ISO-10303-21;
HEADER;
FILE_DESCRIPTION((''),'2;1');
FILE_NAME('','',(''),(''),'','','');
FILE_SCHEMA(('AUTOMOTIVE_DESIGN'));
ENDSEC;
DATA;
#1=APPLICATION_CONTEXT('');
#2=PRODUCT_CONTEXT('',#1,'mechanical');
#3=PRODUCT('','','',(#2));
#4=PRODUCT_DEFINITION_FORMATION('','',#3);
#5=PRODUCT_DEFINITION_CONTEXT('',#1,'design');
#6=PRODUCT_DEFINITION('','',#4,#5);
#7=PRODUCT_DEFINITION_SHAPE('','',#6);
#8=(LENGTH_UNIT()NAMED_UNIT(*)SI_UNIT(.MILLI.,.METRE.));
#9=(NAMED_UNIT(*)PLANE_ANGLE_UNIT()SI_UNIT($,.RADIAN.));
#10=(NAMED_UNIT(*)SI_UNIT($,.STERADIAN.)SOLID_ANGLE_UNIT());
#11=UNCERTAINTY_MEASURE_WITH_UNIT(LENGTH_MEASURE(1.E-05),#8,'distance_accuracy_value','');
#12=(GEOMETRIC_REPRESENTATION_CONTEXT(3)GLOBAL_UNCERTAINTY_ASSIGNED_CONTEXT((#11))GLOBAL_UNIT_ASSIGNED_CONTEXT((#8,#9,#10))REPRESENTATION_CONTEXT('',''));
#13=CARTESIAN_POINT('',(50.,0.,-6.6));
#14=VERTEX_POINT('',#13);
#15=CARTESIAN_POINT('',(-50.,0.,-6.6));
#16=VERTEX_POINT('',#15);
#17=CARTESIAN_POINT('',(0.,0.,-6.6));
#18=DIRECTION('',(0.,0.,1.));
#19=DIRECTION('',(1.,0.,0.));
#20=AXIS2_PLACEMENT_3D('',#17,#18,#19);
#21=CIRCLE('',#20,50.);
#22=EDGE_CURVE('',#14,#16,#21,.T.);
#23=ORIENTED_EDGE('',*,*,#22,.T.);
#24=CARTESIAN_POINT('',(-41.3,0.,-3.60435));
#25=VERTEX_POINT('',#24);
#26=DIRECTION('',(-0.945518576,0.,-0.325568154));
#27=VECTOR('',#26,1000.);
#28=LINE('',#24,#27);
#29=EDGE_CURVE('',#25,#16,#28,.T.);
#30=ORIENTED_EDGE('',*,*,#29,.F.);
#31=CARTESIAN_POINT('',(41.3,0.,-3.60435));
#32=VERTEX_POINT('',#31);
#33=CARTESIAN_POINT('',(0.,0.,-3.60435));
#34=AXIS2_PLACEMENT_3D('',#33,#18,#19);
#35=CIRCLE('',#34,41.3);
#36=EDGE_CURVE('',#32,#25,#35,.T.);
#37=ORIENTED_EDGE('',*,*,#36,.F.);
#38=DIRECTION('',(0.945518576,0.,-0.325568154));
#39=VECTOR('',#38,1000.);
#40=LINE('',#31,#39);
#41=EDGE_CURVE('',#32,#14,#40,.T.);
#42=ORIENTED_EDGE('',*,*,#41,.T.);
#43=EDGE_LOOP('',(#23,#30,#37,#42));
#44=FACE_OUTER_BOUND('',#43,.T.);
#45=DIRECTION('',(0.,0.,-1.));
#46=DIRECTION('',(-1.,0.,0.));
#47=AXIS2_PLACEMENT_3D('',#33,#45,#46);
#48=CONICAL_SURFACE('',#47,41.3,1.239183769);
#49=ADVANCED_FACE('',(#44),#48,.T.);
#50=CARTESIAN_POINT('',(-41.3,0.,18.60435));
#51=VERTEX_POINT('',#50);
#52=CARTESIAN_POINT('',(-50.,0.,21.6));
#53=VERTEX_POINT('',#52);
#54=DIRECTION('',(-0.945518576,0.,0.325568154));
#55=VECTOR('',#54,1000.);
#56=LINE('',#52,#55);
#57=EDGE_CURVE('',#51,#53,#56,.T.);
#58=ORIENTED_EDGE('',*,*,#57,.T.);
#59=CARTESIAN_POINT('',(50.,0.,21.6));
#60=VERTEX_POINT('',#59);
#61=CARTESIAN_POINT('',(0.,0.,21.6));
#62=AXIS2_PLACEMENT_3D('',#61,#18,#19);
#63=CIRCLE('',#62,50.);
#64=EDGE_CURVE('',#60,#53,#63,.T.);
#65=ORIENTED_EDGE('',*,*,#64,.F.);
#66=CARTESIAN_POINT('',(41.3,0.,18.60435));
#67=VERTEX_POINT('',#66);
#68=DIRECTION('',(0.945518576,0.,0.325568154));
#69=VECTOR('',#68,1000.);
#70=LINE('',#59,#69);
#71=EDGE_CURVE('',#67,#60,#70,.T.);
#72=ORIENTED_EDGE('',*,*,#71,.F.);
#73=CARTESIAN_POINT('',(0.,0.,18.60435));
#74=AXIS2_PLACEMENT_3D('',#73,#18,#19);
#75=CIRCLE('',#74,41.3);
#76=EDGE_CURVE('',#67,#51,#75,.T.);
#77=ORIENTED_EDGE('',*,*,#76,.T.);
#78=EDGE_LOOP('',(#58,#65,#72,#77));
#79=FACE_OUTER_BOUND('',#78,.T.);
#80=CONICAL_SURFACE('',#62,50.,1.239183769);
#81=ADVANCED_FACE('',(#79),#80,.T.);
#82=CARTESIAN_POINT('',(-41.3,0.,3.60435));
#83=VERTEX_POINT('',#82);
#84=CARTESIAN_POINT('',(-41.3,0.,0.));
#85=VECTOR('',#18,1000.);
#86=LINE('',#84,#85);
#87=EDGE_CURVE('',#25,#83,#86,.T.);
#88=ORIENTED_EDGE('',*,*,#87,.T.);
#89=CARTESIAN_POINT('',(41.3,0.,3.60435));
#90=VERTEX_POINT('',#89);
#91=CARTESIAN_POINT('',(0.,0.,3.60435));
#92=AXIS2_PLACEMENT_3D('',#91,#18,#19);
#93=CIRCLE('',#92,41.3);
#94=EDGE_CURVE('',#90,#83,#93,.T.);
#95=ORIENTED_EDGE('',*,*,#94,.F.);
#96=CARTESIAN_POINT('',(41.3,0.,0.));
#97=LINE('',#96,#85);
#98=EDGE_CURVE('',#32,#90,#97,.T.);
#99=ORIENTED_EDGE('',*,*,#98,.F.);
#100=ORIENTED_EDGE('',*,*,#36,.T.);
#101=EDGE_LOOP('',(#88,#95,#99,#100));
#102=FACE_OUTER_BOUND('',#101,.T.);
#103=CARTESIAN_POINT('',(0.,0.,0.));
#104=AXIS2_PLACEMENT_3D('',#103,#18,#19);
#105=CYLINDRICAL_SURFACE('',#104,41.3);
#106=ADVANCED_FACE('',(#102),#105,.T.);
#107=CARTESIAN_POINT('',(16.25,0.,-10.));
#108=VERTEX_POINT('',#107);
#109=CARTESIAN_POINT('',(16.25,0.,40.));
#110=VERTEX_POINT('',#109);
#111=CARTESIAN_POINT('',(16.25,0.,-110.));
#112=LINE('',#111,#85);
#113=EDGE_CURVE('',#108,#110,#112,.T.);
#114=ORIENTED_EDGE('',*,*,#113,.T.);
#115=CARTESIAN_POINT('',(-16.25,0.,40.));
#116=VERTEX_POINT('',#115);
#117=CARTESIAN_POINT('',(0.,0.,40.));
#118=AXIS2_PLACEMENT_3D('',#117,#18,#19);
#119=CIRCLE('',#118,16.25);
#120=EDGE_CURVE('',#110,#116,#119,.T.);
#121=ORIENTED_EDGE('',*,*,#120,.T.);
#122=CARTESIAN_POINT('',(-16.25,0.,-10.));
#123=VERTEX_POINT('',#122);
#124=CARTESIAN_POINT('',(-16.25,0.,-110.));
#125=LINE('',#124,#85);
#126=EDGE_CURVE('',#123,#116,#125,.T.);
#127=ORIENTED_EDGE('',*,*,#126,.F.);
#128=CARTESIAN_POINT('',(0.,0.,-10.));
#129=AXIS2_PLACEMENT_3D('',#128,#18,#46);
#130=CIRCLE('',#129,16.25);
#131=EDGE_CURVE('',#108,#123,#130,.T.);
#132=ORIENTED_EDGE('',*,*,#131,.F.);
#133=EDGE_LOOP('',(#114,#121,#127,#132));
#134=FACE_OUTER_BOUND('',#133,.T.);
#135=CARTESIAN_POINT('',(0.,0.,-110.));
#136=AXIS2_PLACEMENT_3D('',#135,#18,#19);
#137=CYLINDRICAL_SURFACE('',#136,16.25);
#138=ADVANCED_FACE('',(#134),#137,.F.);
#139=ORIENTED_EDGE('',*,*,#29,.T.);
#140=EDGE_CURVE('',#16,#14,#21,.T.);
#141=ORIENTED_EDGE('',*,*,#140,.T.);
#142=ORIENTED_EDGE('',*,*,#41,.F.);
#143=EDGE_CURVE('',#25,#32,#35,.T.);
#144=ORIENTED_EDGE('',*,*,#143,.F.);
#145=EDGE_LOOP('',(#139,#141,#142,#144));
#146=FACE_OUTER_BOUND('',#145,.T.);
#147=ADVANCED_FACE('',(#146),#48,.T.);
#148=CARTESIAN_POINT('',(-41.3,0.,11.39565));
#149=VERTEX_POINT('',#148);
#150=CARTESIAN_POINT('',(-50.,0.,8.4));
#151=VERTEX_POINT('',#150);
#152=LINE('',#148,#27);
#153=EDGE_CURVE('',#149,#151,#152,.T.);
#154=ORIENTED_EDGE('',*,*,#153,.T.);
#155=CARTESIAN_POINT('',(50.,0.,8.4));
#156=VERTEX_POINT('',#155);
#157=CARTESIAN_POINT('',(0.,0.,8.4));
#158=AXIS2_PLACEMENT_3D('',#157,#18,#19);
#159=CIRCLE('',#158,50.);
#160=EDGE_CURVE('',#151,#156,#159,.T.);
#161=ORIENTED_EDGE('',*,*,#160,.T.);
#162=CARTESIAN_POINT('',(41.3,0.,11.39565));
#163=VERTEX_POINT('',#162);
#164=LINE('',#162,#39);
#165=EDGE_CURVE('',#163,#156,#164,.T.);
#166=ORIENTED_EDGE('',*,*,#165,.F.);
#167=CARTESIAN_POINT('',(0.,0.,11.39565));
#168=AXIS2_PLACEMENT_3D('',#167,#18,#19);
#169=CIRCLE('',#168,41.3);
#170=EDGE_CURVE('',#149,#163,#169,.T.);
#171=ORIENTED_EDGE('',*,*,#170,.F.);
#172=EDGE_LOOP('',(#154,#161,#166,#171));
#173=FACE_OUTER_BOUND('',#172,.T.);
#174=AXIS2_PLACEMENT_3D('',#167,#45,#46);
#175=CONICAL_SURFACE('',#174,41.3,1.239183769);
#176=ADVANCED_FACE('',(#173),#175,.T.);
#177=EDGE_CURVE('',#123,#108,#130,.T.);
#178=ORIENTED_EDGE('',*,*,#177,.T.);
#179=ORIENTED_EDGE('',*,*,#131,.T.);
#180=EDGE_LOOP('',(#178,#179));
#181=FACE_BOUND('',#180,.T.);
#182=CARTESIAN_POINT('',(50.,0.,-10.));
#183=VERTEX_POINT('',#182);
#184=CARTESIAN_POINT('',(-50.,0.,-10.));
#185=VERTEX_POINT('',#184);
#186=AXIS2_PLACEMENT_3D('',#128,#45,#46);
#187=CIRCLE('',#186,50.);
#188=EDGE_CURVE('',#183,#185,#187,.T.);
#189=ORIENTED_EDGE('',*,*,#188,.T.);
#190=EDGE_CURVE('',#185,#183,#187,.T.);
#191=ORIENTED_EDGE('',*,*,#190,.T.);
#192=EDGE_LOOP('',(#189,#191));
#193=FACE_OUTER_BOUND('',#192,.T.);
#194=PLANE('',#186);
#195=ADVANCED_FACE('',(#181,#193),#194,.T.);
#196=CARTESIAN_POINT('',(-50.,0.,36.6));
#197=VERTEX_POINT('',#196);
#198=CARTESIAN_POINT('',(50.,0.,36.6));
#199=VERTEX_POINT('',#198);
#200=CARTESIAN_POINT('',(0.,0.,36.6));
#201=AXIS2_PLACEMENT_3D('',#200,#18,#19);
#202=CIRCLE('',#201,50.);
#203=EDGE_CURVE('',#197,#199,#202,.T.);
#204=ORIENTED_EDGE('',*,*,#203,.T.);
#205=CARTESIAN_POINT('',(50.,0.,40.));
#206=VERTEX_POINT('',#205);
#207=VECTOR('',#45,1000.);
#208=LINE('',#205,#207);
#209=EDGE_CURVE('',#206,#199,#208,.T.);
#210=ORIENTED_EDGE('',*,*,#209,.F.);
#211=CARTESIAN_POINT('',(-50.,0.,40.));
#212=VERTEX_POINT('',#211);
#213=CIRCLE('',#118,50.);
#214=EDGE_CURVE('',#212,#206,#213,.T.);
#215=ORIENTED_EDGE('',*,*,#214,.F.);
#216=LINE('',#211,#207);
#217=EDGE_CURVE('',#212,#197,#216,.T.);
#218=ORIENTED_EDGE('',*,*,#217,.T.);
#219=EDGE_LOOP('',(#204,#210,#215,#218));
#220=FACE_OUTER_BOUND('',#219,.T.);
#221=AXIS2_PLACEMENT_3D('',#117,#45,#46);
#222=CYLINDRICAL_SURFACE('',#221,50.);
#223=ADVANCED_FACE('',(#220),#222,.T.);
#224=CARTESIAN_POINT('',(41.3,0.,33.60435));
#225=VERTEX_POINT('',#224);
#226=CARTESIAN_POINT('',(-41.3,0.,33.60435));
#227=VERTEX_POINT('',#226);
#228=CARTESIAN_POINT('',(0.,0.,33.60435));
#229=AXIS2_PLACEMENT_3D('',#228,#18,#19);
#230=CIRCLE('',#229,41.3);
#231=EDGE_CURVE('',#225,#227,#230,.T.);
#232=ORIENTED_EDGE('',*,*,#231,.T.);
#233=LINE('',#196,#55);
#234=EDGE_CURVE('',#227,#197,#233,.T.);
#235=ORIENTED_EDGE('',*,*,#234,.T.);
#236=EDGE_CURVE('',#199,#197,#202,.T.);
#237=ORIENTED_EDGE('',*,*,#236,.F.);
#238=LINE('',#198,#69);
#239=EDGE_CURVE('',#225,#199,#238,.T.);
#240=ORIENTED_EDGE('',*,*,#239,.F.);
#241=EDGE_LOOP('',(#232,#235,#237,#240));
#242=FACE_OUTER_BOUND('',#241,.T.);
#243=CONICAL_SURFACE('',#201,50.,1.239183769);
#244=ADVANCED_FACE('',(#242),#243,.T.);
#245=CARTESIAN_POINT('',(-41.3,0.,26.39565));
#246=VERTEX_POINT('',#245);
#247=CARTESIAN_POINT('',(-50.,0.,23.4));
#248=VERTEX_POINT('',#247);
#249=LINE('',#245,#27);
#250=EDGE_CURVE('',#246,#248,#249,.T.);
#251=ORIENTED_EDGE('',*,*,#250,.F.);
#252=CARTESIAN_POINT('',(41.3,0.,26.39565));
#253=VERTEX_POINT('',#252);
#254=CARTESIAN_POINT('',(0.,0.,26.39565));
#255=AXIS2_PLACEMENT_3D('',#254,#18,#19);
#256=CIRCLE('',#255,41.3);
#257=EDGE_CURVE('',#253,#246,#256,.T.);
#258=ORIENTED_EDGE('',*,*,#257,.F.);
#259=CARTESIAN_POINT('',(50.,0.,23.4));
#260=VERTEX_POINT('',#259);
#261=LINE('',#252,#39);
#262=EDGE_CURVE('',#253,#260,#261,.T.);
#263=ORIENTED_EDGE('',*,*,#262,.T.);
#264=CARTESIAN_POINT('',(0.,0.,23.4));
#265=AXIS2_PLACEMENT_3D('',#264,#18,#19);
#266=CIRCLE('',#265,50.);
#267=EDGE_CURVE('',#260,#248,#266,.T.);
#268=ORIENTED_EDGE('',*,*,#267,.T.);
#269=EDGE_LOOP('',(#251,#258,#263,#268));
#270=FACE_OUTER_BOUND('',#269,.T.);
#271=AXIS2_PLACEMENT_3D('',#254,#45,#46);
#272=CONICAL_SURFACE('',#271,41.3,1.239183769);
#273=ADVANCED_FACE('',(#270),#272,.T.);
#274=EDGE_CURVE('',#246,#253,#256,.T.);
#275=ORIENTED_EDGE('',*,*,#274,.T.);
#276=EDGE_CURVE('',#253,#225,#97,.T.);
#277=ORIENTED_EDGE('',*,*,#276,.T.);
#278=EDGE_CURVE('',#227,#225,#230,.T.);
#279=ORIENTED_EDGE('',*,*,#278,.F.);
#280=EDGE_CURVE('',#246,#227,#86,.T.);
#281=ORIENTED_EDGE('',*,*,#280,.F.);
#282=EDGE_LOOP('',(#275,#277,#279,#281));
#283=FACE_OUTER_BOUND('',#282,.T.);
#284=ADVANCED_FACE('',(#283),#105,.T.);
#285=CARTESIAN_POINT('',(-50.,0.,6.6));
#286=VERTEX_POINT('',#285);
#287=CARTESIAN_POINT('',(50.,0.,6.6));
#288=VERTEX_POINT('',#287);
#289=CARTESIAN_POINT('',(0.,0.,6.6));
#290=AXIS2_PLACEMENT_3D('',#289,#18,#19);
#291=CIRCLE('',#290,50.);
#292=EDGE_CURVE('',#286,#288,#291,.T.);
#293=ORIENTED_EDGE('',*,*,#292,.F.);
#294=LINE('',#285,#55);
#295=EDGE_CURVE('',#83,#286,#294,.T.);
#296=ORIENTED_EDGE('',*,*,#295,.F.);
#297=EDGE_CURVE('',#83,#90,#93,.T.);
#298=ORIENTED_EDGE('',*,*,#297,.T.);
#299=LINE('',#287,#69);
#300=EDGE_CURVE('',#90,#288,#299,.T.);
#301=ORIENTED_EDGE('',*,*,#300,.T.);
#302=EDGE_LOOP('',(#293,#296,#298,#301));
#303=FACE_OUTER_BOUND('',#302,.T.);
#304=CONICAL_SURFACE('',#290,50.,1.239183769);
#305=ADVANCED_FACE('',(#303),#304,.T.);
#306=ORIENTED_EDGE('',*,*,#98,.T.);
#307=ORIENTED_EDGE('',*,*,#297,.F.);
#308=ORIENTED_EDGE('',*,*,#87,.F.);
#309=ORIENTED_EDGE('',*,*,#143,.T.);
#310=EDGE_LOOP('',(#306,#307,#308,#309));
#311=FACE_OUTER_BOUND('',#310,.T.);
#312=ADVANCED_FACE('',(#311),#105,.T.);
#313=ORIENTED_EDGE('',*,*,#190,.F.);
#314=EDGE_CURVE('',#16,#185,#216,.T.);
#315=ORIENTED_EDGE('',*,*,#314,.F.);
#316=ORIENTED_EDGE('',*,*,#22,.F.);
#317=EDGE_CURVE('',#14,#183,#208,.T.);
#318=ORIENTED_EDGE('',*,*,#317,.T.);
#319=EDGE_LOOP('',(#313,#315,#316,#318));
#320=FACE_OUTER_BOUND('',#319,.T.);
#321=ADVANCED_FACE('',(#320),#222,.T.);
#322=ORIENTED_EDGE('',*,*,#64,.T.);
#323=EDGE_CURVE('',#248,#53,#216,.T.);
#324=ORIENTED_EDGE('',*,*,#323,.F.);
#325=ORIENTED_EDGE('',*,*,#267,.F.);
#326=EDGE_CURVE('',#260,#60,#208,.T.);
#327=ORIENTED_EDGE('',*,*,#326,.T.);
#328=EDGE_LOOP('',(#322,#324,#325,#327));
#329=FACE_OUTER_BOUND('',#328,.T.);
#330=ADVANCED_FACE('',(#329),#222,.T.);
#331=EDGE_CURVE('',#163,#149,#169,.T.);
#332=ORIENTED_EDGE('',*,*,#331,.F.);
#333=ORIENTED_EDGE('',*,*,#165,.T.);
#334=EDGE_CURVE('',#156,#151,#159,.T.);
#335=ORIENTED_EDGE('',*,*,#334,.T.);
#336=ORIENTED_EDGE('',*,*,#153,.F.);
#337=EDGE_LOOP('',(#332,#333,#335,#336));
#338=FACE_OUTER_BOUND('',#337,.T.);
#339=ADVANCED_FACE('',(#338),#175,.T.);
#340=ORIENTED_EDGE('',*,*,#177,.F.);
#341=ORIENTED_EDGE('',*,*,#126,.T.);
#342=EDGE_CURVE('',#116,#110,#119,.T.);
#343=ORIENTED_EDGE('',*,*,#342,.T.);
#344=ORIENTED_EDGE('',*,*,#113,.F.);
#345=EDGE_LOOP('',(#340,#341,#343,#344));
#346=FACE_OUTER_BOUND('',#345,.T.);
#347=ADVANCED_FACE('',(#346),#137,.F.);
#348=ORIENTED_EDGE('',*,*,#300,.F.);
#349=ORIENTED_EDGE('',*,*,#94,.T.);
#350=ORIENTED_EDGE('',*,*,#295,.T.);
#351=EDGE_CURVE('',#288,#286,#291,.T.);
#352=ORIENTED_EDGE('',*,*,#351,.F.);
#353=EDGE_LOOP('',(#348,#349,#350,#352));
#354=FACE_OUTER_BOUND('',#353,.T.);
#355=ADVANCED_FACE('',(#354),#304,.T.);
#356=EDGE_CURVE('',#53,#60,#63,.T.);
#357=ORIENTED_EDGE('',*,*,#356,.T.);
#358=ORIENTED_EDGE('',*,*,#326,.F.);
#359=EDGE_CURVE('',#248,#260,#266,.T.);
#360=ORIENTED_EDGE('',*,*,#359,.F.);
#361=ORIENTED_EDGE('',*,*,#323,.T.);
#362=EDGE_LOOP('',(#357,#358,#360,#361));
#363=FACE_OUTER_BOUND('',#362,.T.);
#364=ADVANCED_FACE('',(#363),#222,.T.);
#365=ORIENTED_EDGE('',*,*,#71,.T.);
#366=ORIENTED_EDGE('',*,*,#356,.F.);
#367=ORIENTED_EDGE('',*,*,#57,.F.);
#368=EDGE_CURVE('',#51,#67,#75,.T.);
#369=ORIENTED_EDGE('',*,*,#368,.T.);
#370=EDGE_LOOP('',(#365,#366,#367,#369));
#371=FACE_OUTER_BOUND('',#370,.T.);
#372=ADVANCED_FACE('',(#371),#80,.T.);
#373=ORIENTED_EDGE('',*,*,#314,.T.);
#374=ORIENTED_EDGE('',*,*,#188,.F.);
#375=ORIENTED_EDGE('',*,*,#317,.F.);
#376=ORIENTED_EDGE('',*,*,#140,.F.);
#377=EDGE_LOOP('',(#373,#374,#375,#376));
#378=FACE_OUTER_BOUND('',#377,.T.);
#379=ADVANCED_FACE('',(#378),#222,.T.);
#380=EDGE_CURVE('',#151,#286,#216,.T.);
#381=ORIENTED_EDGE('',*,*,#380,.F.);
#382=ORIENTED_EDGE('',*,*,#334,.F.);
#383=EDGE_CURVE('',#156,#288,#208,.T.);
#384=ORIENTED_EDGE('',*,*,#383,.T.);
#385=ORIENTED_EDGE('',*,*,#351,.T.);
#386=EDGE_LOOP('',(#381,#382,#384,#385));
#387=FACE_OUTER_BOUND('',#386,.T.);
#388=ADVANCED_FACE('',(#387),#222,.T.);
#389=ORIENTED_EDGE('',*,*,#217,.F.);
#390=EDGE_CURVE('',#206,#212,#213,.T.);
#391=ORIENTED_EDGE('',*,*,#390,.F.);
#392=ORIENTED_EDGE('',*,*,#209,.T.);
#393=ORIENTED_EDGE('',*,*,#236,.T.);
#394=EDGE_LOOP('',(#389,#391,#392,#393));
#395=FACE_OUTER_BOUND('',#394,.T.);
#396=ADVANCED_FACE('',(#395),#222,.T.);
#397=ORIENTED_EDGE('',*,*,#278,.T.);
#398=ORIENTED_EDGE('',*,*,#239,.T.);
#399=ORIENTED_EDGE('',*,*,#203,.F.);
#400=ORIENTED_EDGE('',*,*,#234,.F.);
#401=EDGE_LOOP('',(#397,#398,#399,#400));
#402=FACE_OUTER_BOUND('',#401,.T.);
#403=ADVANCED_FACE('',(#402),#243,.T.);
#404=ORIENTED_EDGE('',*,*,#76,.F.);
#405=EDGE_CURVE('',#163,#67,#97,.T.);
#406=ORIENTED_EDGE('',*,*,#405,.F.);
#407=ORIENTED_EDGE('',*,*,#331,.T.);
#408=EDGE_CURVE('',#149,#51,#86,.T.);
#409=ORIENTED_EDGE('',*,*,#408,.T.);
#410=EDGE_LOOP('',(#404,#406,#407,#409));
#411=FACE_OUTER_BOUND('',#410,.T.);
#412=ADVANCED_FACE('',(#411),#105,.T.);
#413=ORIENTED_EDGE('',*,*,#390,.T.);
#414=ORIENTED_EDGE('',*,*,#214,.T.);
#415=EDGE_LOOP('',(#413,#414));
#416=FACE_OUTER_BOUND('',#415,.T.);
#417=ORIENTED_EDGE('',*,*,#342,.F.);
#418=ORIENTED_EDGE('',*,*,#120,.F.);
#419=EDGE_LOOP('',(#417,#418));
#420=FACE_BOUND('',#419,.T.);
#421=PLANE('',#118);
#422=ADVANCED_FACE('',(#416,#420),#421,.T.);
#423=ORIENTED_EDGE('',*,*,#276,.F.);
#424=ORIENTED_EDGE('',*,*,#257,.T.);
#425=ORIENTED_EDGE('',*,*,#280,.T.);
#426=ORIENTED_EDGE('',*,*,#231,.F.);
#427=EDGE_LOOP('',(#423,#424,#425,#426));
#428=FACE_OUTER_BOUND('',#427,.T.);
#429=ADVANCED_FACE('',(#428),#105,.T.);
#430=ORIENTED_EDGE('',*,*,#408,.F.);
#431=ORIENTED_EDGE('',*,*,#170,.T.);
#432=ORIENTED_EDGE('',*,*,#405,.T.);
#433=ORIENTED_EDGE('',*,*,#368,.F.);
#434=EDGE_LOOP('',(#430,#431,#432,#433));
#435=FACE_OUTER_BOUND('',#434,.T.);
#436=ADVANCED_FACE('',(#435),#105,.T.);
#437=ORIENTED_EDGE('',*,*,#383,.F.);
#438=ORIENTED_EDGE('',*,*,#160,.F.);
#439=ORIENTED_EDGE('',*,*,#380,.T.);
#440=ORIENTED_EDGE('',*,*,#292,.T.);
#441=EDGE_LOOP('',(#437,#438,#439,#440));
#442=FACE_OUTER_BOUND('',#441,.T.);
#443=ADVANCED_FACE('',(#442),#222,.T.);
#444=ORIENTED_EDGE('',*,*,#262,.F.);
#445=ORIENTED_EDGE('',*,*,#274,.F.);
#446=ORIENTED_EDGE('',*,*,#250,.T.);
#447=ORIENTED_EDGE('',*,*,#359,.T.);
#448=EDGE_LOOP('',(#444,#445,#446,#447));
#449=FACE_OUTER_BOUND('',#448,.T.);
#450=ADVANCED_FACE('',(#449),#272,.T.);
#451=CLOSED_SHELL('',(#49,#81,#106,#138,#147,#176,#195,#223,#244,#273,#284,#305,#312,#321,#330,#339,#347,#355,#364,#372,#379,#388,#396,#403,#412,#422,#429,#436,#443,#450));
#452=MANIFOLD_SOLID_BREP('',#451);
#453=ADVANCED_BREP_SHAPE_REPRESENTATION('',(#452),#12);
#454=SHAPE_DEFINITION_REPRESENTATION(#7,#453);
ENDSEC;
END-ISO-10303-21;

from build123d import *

# Parameters (mm, degrees)
SKETCH1_R           = 50
BOSS_EXTRUDE1_DEPTH = 40
SKETCH2_R           = 16.25
CUT_EXTRUDE1_DEPTH  = 150
SKETCH10_R          = 100
CUT_EXTRUDE5_DEPTH  = 20
SKETCH11_R          = 30
SKETCH11_R_2        = 16.25
BOSS_EXTRUDE2_DEPTH = 20
SKETCH12_R          = 130
CUT_EXTRUDE7_DEPTH  = 30


with BuildPart() as part:
    # Sketch1 → Boss-Extrude1 (new, symmetric)
    with BuildSketch(Plane.XY):
        Circle(SKETCH1_R)
    extrude(amount=BOSS_EXTRUDE1_DEPTH, both=True)

    # Sketch2 → Cut-Extrude1 (cut)
    with BuildSketch(Plane.XY.offset(40)):
        Circle(SKETCH2_R)
    extrude(amount=-CUT_EXTRUDE1_DEPTH, mode=Mode.SUBTRACT)

    # Sketch4 → Cut-Revolve1 (revolve, cut)
    with BuildSketch(Plane(origin=(0, 0, 0), x_dir=(0, 0, -1), z_dir=(1, 0, 0)), mode=Mode.PRIVATE) as cut_revolve1_sk:
        Polygon((-40, 50), (-36.6, 50), (-33.604349764, 41.3), (-26.395650236, 41.3), (-23.4, 50), (-21.6, 50), (-18.604349764, 41.3), (-11.395650236, 41.3), (-8.4, 50), (-6.6, 50), (-3.604349764, 41.3), (3.604349764, 41.3), (6.6, 50), (10, 50), (10, 161.050459045), (-40, 161.050459045), align=None)
    revolve(cut_revolve1_sk.sketch.rotate(Axis((0, 0, 0), (0, 0, -1)), 90), axis=Axis((0, 0, 0), (0, 0, -1)), mode=Mode.SUBTRACT)

    # Sketch10 → Cut-Extrude5 (cut)
    with BuildSketch(Plane(origin=(0, 0, -40), x_dir=(-1, 0, 0), z_dir=(0, 0, -1))):
        Circle(SKETCH10_R)
    extrude(amount=-CUT_EXTRUDE5_DEPTH, mode=Mode.SUBTRACT)

    # Sketch11 → Boss-Extrude2 (add)
    with BuildSketch(Plane(origin=(0, 0, -20), x_dir=(-1, 0, 0), z_dir=(0, 0, -1))):
        Circle(SKETCH11_R)
        with Locations(Location((0, 0, 0), (0, 0, 180))):
            Circle(SKETCH11_R_2, mode=Mode.SUBTRACT)
    extrude(amount=BOSS_EXTRUDE2_DEPTH)

    # Sketch12 → Cut-Extrude7 (cut)
    with BuildSketch(Plane(origin=(0, 0, -40), x_dir=(-1, 0, 0), z_dir=(0, 0, -1))):
        Circle(SKETCH12_R)
    extrude(amount=-CUT_EXTRUDE7_DEPTH, mode=Mode.SUBTRACT)


solid = part.part
